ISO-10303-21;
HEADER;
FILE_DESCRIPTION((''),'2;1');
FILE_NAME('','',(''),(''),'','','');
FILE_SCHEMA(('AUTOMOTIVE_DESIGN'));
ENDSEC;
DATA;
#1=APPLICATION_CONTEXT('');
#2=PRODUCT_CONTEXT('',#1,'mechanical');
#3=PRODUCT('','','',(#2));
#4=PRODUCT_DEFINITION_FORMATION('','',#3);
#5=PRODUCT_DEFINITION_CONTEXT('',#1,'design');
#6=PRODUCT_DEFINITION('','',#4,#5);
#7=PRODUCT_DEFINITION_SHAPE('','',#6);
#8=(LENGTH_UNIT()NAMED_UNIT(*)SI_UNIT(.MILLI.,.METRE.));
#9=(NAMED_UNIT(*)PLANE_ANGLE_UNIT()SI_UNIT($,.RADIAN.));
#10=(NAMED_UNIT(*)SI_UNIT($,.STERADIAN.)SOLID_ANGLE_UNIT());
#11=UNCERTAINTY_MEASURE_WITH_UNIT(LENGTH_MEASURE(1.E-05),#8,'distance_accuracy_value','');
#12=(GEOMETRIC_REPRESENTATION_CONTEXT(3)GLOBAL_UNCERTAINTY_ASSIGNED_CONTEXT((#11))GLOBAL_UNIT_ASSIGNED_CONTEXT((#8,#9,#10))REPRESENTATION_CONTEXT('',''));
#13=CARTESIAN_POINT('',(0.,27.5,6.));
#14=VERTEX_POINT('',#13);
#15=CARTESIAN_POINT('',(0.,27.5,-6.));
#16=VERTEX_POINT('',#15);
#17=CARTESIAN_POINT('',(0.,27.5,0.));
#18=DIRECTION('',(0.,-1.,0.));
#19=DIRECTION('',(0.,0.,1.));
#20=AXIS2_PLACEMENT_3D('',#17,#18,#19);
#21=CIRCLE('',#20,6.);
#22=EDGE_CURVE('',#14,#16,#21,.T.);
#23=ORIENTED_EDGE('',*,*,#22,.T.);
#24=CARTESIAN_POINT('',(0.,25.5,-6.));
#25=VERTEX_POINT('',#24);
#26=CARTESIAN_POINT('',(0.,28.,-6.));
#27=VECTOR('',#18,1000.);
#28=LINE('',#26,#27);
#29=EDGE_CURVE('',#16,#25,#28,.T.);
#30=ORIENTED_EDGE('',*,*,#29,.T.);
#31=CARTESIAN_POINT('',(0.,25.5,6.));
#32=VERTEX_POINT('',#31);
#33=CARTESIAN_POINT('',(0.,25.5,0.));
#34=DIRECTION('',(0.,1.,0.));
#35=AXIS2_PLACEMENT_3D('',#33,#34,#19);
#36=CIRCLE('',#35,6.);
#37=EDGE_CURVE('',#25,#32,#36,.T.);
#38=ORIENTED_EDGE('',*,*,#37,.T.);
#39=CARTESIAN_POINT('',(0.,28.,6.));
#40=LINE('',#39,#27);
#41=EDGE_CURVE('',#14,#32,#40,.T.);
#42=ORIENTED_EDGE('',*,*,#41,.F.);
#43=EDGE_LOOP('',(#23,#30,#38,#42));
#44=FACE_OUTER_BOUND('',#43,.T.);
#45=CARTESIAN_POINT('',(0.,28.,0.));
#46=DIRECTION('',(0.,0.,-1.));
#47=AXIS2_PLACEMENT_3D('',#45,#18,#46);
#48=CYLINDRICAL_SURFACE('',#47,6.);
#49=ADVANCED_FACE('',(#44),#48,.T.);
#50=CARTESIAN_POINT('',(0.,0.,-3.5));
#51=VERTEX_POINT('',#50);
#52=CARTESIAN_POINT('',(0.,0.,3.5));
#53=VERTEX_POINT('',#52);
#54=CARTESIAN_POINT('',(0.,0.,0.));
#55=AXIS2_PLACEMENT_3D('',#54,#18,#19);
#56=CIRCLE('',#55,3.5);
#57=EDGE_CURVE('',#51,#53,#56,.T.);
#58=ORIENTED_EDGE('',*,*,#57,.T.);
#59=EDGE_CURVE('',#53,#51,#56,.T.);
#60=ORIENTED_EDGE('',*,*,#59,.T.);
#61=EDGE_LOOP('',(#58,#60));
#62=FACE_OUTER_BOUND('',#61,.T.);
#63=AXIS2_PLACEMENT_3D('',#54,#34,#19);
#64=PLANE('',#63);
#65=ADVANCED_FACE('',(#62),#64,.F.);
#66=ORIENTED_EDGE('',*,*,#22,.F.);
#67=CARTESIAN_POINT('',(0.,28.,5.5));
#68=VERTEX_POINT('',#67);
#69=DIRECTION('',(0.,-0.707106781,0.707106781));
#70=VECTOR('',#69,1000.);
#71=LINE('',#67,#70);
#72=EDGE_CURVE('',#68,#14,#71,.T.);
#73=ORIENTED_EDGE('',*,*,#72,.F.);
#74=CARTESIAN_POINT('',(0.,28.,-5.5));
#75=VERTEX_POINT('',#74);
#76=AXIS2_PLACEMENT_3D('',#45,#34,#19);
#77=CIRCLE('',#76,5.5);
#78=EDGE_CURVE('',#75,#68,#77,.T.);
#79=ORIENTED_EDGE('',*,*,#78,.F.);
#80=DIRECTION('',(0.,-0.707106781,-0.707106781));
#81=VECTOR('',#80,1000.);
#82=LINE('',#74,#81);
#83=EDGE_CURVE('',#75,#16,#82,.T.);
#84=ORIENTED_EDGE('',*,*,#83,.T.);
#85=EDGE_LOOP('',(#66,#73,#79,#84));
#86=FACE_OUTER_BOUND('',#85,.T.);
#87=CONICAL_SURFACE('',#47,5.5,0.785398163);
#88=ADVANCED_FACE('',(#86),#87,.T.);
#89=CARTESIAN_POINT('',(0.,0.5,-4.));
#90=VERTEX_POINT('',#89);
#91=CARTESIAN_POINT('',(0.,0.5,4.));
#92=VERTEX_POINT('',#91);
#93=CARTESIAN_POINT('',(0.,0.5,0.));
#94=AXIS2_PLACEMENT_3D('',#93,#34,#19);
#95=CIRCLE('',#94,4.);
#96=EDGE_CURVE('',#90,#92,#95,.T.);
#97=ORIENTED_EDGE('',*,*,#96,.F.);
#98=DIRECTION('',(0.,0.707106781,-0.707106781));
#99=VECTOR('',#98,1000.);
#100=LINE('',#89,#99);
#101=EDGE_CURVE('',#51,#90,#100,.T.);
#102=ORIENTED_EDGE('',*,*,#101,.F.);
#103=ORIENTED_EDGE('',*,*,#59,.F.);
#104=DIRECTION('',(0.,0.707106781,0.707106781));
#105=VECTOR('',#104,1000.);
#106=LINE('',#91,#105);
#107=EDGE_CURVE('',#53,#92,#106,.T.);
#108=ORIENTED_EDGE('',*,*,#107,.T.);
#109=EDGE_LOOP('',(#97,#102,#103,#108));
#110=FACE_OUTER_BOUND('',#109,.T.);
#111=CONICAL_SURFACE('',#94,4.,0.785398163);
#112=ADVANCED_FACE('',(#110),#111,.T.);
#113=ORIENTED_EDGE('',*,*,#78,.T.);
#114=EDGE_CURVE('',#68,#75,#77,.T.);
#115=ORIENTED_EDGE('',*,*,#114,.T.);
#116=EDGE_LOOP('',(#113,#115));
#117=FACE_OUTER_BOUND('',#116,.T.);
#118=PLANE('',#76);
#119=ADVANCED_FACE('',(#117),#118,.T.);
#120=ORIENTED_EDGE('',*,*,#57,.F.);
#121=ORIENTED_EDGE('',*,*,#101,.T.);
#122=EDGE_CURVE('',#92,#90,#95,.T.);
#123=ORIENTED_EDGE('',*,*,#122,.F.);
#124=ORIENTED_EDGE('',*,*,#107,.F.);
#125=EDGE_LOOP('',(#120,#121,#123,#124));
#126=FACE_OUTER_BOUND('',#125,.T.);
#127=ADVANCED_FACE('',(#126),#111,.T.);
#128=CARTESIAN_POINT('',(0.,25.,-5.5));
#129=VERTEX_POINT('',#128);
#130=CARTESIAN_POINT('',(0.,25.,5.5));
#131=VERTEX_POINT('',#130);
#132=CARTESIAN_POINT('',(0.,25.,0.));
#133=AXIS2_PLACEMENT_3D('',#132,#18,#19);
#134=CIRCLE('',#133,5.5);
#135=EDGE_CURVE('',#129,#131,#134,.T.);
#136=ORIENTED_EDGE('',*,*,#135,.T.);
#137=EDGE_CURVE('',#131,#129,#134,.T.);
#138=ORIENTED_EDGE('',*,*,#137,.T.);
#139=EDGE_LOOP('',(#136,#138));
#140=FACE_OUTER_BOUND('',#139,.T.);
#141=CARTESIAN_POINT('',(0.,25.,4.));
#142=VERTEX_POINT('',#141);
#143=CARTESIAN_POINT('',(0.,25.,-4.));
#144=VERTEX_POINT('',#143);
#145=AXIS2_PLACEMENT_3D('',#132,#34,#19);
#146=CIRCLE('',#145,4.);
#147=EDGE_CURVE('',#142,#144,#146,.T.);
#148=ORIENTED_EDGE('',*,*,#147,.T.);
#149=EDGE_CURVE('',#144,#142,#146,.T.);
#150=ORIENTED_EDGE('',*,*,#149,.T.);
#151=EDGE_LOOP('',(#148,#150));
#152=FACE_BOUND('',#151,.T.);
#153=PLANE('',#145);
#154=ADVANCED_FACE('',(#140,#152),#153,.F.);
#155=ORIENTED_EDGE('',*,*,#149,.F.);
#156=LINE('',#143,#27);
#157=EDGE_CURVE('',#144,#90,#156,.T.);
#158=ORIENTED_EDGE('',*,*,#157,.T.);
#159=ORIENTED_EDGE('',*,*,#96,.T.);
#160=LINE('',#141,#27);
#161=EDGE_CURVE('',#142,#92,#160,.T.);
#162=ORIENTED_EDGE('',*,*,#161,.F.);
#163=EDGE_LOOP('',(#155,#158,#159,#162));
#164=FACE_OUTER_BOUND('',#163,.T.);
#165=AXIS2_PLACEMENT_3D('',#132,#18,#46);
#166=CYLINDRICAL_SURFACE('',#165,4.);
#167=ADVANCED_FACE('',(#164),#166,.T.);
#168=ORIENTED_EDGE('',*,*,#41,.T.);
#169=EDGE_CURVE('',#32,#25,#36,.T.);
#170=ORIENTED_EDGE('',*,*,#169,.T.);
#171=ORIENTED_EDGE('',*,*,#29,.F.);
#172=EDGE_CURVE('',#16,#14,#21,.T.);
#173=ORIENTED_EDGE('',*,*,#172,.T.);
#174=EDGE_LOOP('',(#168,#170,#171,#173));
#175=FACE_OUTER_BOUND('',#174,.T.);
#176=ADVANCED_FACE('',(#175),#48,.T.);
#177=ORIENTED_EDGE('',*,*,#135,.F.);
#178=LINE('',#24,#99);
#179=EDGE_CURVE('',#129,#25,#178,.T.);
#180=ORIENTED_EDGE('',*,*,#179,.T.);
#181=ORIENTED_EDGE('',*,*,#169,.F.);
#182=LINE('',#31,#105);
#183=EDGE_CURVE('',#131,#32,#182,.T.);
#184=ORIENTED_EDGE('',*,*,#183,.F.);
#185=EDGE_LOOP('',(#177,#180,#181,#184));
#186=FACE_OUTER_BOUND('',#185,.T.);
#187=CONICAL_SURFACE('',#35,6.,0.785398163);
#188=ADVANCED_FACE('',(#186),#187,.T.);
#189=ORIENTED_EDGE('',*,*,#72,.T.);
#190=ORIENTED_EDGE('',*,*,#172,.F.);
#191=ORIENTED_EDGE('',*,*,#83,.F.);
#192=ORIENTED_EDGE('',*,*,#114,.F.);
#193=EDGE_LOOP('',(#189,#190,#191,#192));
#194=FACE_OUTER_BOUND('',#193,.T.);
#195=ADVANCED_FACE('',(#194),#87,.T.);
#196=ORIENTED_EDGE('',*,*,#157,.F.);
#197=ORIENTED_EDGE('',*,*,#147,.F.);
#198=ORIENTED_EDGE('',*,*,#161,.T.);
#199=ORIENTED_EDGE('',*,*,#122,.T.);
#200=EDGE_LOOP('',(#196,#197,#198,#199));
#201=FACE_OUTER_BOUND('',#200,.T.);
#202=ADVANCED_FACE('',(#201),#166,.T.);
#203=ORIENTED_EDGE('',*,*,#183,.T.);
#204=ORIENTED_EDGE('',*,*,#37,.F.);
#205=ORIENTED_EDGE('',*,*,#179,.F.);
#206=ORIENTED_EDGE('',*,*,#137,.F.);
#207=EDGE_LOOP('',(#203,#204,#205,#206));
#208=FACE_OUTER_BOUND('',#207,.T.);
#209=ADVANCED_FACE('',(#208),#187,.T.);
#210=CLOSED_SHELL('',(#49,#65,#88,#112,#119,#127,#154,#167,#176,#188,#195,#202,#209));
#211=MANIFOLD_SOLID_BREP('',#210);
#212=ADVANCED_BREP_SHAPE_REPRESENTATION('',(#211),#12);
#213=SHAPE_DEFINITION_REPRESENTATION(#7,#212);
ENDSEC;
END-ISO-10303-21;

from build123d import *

# Parameters (mm, degrees)
SKETCH2_R           = 4
BOSS_EXTRUDE1_DEPTH = 25
SKETCH3_R           = 6
BOSS_EXTRUDE2_DEPTH = 3
CHAMFER1_SIZE       = 0.5


with BuildPart() as part:
    # Sketch2 → Boss-Extrude1 (new body)
    with BuildSketch(Plane(origin=(0, 0, 0), x_dir=(1, 0, 0), z_dir=(0, 1, 0))):
        with Locations(Location((0, 0, 0), (0, 0, 270))):
            Circle(SKETCH2_R)
    extrude(amount=BOSS_EXTRUDE1_DEPTH)

    # Sketch3 → Boss-Extrude2 (add)
    with BuildSketch(Plane(origin=(0, 25, 0), x_dir=(1, 0, 0), z_dir=(0, 1, 0))):
        with Locations(Location((0, 0, 0), (0, 0, 270))):
            Circle(SKETCH3_R)
    extrude(amount=BOSS_EXTRUDE2_DEPTH)

    # Chamfer1
    chamfer1_edges = [part.edges().sort_by_distance(p)[0] for p in [
        (0, 0, -4),
        (0, 25, -6),
        (0, 28, -6),
    ]]
    chamfer(chamfer1_edges, length=CHAMFER1_SIZE)


solid = part.part
